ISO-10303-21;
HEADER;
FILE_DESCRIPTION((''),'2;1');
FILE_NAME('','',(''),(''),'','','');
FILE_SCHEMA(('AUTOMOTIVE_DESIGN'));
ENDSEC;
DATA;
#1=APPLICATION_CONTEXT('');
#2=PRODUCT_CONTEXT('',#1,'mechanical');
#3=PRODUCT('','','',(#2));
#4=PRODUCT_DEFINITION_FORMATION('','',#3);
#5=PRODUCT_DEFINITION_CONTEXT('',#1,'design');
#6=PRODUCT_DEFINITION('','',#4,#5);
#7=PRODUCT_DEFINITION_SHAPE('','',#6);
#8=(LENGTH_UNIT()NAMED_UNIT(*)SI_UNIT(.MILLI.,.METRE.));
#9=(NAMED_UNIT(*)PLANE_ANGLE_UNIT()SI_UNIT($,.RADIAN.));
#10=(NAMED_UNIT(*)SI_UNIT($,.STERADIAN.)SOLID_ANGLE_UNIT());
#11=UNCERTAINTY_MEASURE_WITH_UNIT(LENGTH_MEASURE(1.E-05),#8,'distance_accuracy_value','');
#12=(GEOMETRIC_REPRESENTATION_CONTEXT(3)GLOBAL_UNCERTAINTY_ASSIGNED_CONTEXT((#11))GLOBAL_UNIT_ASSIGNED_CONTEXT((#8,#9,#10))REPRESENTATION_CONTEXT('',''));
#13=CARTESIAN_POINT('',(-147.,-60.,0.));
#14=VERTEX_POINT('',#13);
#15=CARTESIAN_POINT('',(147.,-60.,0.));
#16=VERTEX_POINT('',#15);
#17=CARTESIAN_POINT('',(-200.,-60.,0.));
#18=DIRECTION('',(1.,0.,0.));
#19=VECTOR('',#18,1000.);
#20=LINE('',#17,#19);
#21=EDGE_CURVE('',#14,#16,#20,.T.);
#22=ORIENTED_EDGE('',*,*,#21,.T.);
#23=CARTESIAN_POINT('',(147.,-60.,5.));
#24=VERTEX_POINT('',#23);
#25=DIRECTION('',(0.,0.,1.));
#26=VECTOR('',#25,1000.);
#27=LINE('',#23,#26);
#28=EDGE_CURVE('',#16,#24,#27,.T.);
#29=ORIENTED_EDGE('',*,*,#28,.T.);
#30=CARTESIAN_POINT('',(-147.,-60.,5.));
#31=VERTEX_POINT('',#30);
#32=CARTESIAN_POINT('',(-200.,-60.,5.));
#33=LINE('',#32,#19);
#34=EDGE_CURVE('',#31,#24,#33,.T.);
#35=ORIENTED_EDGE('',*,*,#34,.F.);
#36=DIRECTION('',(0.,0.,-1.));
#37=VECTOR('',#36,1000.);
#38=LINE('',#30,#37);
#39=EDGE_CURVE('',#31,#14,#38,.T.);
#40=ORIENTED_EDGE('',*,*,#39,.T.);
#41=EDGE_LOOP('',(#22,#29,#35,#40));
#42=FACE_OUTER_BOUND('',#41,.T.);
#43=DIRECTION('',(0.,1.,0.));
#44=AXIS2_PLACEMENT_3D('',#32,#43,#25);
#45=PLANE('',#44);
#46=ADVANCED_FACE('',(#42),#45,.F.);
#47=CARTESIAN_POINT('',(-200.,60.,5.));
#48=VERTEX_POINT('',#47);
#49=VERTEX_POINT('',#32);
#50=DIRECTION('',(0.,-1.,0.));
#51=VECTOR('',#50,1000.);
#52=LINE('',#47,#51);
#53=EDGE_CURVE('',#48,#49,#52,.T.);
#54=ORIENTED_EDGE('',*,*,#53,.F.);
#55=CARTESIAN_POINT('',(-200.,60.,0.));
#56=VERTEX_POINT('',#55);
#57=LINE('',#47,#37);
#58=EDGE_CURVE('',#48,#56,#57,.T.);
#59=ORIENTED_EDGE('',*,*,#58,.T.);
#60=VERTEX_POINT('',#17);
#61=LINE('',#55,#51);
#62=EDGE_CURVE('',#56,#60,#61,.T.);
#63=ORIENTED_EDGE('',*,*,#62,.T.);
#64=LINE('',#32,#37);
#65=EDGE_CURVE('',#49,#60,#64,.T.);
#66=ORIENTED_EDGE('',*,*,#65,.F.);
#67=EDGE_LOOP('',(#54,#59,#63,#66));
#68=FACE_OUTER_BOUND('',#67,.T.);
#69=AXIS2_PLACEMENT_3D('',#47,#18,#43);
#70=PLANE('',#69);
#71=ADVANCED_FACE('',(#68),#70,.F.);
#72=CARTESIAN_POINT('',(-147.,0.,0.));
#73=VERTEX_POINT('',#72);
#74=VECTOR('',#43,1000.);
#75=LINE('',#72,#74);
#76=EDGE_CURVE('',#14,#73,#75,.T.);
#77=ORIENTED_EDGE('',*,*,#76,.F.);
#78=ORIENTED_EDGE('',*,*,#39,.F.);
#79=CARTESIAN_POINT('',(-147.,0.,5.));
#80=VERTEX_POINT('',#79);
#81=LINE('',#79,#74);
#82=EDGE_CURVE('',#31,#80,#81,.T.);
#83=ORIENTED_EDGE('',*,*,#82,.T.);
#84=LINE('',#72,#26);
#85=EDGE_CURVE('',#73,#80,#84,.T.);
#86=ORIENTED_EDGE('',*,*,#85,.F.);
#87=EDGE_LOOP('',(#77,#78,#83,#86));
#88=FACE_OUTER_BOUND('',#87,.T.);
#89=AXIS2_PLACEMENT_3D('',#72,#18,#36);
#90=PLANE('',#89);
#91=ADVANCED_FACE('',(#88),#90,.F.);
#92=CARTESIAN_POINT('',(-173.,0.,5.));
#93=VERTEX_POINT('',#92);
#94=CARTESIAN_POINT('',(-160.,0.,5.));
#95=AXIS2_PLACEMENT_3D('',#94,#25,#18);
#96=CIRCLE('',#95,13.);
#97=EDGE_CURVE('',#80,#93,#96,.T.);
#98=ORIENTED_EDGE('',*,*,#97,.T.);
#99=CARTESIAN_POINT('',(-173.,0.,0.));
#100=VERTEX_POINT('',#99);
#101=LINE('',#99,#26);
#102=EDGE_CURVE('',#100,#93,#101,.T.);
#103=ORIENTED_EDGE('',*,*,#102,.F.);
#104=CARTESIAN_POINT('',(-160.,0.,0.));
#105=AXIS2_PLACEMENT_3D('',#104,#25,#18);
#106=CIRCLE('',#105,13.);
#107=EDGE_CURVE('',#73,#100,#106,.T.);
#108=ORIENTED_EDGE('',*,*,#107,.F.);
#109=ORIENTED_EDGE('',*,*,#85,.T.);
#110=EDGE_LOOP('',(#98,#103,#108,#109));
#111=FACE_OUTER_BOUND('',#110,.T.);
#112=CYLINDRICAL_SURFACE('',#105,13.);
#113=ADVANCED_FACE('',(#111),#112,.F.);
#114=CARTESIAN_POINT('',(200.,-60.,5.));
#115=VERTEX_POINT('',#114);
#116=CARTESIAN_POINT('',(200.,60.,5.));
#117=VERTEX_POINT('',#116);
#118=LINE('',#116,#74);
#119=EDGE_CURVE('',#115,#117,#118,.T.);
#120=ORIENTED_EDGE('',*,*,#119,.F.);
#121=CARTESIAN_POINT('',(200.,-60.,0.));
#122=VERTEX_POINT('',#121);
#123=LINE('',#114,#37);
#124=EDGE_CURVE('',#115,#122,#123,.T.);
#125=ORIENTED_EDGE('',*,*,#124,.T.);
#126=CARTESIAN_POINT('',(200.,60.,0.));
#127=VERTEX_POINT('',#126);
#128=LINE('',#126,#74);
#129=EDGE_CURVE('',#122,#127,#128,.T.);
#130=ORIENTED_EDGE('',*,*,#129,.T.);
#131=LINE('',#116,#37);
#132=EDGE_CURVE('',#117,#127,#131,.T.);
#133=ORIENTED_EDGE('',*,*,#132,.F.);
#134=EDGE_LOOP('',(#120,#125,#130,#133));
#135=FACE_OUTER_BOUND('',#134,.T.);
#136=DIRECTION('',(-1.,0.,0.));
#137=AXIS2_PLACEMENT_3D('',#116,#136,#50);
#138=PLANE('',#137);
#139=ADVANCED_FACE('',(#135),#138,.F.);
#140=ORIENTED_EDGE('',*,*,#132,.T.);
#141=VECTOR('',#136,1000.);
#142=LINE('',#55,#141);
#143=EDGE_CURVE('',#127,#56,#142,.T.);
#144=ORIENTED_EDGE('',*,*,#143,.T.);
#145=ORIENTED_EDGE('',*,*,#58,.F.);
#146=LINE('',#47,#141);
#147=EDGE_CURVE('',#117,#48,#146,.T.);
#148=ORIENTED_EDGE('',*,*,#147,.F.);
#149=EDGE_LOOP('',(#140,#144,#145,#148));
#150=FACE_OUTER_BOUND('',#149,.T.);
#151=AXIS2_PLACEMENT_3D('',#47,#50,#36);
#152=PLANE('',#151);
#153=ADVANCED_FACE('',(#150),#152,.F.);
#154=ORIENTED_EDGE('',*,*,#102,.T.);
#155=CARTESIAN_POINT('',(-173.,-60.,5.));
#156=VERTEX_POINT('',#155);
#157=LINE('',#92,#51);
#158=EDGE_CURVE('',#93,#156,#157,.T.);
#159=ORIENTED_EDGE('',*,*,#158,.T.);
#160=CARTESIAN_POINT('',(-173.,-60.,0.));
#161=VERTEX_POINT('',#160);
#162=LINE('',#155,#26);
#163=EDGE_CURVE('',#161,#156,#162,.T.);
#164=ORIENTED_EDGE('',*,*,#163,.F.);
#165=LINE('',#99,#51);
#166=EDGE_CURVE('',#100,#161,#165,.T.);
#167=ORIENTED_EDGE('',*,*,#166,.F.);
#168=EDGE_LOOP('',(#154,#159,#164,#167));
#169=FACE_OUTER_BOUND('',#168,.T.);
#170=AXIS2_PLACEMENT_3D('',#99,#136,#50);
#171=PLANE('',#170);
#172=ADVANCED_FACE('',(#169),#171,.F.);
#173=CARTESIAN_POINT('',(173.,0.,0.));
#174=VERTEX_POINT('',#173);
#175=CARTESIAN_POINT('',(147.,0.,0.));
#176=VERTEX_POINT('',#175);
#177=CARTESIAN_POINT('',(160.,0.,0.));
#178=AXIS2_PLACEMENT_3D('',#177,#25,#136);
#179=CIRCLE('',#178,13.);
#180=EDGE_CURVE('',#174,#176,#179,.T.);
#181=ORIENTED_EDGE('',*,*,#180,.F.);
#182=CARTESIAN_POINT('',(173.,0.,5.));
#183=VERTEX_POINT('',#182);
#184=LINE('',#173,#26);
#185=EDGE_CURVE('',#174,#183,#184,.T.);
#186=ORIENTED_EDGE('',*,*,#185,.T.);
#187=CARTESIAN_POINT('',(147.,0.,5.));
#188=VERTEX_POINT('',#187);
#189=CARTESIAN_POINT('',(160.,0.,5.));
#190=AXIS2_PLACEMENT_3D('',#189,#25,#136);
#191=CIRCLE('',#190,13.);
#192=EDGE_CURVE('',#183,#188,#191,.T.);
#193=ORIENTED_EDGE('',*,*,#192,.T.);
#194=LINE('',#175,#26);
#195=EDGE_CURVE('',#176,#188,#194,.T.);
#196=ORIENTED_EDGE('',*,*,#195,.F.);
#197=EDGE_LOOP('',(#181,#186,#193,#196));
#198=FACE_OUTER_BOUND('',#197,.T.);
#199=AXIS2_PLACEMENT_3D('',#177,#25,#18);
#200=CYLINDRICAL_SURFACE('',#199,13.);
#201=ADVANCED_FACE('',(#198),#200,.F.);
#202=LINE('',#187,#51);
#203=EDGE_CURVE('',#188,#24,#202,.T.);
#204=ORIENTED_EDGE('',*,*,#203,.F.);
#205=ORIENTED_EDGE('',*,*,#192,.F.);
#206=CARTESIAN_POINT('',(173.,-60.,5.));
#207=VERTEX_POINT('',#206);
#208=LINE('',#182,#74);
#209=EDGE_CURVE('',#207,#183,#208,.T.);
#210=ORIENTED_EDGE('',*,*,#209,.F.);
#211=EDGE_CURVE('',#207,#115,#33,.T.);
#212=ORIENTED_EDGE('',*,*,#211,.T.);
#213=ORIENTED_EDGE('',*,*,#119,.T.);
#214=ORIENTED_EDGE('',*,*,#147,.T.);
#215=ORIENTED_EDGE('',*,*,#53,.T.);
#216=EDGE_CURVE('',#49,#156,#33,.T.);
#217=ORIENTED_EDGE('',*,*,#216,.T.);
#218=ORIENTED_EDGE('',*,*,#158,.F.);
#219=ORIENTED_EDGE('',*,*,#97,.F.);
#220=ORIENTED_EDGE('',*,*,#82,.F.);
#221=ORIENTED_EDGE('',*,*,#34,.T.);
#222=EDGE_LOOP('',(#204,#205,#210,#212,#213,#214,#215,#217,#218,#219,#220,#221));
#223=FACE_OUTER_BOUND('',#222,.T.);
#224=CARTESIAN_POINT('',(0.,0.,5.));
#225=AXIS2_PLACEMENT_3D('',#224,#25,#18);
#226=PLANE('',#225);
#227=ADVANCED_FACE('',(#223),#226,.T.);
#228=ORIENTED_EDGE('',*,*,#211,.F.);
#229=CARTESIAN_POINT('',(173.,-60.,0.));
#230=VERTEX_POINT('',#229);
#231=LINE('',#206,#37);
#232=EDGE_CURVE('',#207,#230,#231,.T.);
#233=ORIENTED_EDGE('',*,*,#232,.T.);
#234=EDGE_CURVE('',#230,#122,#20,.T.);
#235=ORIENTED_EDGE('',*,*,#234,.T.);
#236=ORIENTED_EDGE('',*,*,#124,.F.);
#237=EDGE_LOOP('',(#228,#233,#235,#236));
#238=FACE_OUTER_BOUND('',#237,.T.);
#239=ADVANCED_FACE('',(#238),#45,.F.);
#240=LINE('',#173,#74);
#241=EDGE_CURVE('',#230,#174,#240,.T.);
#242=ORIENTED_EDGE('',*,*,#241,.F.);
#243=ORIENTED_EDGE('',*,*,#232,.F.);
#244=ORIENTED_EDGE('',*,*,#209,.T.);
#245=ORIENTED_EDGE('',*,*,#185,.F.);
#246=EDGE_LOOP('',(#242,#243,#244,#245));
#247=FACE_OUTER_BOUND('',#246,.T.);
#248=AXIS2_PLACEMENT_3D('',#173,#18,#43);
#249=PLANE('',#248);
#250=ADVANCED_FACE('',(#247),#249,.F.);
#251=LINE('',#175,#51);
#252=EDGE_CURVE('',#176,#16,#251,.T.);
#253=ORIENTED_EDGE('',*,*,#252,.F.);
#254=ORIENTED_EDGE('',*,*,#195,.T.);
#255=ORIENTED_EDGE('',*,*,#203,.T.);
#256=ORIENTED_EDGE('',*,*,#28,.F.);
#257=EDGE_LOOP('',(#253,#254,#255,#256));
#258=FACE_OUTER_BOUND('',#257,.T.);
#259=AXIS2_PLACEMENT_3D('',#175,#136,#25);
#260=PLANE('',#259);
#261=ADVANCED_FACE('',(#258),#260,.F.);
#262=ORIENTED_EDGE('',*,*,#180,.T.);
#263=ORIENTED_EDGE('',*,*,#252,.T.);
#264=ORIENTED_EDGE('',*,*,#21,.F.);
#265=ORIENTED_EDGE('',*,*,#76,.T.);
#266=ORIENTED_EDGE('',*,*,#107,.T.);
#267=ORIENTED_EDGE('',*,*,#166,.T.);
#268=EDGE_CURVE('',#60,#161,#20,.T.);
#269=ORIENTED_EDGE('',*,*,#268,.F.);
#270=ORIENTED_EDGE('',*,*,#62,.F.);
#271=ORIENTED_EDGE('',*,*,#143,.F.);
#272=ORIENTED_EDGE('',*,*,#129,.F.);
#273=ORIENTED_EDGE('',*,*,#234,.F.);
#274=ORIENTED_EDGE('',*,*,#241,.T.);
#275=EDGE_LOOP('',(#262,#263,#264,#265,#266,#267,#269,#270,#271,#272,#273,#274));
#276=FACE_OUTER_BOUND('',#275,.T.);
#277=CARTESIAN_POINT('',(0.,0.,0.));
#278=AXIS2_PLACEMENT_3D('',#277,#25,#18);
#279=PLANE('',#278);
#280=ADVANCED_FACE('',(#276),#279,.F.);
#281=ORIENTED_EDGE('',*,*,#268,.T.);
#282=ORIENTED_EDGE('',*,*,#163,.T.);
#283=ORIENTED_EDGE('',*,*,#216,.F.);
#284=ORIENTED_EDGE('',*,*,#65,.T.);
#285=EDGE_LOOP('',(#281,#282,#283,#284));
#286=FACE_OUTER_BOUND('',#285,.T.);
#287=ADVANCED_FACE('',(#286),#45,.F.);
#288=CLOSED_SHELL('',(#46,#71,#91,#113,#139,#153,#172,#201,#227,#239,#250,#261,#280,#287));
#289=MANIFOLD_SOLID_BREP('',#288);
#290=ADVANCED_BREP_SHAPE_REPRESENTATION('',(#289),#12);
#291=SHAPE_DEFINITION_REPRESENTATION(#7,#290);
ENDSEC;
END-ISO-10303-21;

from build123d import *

# Parameters (mm, degrees)
SKETCH1_W           = 400
SKETCH1_H           = 120
BOSS_EXTRUDE1_DEPTH = 5
CUT_EXTRUDE1_DEPTH  = 209.865985742


with BuildPart() as part:
    # Sketch1 → Boss-Extrude1 (new body)
    with BuildSketch(Plane.XY):
        Rectangle(SKETCH1_W, SKETCH1_H)
    extrude(amount=BOSS_EXTRUDE1_DEPTH)

    # Sketch2 → Cut-Extrude1 (cut, through all)
    with BuildSketch(Plane.XY.offset(5)):
        with BuildLine():
            Line((-147, 0), (-147, -96.926835552))
            ThreePointArc((-147, -96.926835552), (-160, -109.926835552), (-173, -96.926835552))
            Line((-173, -96.926835552), (-173, 0))
            ThreePointArc((-173, 0), (-160, 13), (-147, 0))
        make_face()
        with BuildLine():
            Line((147, 0), (147, -96.926835552))
            ThreePointArc((147, -96.926835552), (160, -109.926835552), (173, -96.926835552))
            Line((173, -96.926835552), (173, 0))
            ThreePointArc((173, 0), (160, 13), (147, 0))
        make_face()
    extrude(amount=-CUT_EXTRUDE1_DEPTH, mode=Mode.SUBTRACT)


solid = part.part
